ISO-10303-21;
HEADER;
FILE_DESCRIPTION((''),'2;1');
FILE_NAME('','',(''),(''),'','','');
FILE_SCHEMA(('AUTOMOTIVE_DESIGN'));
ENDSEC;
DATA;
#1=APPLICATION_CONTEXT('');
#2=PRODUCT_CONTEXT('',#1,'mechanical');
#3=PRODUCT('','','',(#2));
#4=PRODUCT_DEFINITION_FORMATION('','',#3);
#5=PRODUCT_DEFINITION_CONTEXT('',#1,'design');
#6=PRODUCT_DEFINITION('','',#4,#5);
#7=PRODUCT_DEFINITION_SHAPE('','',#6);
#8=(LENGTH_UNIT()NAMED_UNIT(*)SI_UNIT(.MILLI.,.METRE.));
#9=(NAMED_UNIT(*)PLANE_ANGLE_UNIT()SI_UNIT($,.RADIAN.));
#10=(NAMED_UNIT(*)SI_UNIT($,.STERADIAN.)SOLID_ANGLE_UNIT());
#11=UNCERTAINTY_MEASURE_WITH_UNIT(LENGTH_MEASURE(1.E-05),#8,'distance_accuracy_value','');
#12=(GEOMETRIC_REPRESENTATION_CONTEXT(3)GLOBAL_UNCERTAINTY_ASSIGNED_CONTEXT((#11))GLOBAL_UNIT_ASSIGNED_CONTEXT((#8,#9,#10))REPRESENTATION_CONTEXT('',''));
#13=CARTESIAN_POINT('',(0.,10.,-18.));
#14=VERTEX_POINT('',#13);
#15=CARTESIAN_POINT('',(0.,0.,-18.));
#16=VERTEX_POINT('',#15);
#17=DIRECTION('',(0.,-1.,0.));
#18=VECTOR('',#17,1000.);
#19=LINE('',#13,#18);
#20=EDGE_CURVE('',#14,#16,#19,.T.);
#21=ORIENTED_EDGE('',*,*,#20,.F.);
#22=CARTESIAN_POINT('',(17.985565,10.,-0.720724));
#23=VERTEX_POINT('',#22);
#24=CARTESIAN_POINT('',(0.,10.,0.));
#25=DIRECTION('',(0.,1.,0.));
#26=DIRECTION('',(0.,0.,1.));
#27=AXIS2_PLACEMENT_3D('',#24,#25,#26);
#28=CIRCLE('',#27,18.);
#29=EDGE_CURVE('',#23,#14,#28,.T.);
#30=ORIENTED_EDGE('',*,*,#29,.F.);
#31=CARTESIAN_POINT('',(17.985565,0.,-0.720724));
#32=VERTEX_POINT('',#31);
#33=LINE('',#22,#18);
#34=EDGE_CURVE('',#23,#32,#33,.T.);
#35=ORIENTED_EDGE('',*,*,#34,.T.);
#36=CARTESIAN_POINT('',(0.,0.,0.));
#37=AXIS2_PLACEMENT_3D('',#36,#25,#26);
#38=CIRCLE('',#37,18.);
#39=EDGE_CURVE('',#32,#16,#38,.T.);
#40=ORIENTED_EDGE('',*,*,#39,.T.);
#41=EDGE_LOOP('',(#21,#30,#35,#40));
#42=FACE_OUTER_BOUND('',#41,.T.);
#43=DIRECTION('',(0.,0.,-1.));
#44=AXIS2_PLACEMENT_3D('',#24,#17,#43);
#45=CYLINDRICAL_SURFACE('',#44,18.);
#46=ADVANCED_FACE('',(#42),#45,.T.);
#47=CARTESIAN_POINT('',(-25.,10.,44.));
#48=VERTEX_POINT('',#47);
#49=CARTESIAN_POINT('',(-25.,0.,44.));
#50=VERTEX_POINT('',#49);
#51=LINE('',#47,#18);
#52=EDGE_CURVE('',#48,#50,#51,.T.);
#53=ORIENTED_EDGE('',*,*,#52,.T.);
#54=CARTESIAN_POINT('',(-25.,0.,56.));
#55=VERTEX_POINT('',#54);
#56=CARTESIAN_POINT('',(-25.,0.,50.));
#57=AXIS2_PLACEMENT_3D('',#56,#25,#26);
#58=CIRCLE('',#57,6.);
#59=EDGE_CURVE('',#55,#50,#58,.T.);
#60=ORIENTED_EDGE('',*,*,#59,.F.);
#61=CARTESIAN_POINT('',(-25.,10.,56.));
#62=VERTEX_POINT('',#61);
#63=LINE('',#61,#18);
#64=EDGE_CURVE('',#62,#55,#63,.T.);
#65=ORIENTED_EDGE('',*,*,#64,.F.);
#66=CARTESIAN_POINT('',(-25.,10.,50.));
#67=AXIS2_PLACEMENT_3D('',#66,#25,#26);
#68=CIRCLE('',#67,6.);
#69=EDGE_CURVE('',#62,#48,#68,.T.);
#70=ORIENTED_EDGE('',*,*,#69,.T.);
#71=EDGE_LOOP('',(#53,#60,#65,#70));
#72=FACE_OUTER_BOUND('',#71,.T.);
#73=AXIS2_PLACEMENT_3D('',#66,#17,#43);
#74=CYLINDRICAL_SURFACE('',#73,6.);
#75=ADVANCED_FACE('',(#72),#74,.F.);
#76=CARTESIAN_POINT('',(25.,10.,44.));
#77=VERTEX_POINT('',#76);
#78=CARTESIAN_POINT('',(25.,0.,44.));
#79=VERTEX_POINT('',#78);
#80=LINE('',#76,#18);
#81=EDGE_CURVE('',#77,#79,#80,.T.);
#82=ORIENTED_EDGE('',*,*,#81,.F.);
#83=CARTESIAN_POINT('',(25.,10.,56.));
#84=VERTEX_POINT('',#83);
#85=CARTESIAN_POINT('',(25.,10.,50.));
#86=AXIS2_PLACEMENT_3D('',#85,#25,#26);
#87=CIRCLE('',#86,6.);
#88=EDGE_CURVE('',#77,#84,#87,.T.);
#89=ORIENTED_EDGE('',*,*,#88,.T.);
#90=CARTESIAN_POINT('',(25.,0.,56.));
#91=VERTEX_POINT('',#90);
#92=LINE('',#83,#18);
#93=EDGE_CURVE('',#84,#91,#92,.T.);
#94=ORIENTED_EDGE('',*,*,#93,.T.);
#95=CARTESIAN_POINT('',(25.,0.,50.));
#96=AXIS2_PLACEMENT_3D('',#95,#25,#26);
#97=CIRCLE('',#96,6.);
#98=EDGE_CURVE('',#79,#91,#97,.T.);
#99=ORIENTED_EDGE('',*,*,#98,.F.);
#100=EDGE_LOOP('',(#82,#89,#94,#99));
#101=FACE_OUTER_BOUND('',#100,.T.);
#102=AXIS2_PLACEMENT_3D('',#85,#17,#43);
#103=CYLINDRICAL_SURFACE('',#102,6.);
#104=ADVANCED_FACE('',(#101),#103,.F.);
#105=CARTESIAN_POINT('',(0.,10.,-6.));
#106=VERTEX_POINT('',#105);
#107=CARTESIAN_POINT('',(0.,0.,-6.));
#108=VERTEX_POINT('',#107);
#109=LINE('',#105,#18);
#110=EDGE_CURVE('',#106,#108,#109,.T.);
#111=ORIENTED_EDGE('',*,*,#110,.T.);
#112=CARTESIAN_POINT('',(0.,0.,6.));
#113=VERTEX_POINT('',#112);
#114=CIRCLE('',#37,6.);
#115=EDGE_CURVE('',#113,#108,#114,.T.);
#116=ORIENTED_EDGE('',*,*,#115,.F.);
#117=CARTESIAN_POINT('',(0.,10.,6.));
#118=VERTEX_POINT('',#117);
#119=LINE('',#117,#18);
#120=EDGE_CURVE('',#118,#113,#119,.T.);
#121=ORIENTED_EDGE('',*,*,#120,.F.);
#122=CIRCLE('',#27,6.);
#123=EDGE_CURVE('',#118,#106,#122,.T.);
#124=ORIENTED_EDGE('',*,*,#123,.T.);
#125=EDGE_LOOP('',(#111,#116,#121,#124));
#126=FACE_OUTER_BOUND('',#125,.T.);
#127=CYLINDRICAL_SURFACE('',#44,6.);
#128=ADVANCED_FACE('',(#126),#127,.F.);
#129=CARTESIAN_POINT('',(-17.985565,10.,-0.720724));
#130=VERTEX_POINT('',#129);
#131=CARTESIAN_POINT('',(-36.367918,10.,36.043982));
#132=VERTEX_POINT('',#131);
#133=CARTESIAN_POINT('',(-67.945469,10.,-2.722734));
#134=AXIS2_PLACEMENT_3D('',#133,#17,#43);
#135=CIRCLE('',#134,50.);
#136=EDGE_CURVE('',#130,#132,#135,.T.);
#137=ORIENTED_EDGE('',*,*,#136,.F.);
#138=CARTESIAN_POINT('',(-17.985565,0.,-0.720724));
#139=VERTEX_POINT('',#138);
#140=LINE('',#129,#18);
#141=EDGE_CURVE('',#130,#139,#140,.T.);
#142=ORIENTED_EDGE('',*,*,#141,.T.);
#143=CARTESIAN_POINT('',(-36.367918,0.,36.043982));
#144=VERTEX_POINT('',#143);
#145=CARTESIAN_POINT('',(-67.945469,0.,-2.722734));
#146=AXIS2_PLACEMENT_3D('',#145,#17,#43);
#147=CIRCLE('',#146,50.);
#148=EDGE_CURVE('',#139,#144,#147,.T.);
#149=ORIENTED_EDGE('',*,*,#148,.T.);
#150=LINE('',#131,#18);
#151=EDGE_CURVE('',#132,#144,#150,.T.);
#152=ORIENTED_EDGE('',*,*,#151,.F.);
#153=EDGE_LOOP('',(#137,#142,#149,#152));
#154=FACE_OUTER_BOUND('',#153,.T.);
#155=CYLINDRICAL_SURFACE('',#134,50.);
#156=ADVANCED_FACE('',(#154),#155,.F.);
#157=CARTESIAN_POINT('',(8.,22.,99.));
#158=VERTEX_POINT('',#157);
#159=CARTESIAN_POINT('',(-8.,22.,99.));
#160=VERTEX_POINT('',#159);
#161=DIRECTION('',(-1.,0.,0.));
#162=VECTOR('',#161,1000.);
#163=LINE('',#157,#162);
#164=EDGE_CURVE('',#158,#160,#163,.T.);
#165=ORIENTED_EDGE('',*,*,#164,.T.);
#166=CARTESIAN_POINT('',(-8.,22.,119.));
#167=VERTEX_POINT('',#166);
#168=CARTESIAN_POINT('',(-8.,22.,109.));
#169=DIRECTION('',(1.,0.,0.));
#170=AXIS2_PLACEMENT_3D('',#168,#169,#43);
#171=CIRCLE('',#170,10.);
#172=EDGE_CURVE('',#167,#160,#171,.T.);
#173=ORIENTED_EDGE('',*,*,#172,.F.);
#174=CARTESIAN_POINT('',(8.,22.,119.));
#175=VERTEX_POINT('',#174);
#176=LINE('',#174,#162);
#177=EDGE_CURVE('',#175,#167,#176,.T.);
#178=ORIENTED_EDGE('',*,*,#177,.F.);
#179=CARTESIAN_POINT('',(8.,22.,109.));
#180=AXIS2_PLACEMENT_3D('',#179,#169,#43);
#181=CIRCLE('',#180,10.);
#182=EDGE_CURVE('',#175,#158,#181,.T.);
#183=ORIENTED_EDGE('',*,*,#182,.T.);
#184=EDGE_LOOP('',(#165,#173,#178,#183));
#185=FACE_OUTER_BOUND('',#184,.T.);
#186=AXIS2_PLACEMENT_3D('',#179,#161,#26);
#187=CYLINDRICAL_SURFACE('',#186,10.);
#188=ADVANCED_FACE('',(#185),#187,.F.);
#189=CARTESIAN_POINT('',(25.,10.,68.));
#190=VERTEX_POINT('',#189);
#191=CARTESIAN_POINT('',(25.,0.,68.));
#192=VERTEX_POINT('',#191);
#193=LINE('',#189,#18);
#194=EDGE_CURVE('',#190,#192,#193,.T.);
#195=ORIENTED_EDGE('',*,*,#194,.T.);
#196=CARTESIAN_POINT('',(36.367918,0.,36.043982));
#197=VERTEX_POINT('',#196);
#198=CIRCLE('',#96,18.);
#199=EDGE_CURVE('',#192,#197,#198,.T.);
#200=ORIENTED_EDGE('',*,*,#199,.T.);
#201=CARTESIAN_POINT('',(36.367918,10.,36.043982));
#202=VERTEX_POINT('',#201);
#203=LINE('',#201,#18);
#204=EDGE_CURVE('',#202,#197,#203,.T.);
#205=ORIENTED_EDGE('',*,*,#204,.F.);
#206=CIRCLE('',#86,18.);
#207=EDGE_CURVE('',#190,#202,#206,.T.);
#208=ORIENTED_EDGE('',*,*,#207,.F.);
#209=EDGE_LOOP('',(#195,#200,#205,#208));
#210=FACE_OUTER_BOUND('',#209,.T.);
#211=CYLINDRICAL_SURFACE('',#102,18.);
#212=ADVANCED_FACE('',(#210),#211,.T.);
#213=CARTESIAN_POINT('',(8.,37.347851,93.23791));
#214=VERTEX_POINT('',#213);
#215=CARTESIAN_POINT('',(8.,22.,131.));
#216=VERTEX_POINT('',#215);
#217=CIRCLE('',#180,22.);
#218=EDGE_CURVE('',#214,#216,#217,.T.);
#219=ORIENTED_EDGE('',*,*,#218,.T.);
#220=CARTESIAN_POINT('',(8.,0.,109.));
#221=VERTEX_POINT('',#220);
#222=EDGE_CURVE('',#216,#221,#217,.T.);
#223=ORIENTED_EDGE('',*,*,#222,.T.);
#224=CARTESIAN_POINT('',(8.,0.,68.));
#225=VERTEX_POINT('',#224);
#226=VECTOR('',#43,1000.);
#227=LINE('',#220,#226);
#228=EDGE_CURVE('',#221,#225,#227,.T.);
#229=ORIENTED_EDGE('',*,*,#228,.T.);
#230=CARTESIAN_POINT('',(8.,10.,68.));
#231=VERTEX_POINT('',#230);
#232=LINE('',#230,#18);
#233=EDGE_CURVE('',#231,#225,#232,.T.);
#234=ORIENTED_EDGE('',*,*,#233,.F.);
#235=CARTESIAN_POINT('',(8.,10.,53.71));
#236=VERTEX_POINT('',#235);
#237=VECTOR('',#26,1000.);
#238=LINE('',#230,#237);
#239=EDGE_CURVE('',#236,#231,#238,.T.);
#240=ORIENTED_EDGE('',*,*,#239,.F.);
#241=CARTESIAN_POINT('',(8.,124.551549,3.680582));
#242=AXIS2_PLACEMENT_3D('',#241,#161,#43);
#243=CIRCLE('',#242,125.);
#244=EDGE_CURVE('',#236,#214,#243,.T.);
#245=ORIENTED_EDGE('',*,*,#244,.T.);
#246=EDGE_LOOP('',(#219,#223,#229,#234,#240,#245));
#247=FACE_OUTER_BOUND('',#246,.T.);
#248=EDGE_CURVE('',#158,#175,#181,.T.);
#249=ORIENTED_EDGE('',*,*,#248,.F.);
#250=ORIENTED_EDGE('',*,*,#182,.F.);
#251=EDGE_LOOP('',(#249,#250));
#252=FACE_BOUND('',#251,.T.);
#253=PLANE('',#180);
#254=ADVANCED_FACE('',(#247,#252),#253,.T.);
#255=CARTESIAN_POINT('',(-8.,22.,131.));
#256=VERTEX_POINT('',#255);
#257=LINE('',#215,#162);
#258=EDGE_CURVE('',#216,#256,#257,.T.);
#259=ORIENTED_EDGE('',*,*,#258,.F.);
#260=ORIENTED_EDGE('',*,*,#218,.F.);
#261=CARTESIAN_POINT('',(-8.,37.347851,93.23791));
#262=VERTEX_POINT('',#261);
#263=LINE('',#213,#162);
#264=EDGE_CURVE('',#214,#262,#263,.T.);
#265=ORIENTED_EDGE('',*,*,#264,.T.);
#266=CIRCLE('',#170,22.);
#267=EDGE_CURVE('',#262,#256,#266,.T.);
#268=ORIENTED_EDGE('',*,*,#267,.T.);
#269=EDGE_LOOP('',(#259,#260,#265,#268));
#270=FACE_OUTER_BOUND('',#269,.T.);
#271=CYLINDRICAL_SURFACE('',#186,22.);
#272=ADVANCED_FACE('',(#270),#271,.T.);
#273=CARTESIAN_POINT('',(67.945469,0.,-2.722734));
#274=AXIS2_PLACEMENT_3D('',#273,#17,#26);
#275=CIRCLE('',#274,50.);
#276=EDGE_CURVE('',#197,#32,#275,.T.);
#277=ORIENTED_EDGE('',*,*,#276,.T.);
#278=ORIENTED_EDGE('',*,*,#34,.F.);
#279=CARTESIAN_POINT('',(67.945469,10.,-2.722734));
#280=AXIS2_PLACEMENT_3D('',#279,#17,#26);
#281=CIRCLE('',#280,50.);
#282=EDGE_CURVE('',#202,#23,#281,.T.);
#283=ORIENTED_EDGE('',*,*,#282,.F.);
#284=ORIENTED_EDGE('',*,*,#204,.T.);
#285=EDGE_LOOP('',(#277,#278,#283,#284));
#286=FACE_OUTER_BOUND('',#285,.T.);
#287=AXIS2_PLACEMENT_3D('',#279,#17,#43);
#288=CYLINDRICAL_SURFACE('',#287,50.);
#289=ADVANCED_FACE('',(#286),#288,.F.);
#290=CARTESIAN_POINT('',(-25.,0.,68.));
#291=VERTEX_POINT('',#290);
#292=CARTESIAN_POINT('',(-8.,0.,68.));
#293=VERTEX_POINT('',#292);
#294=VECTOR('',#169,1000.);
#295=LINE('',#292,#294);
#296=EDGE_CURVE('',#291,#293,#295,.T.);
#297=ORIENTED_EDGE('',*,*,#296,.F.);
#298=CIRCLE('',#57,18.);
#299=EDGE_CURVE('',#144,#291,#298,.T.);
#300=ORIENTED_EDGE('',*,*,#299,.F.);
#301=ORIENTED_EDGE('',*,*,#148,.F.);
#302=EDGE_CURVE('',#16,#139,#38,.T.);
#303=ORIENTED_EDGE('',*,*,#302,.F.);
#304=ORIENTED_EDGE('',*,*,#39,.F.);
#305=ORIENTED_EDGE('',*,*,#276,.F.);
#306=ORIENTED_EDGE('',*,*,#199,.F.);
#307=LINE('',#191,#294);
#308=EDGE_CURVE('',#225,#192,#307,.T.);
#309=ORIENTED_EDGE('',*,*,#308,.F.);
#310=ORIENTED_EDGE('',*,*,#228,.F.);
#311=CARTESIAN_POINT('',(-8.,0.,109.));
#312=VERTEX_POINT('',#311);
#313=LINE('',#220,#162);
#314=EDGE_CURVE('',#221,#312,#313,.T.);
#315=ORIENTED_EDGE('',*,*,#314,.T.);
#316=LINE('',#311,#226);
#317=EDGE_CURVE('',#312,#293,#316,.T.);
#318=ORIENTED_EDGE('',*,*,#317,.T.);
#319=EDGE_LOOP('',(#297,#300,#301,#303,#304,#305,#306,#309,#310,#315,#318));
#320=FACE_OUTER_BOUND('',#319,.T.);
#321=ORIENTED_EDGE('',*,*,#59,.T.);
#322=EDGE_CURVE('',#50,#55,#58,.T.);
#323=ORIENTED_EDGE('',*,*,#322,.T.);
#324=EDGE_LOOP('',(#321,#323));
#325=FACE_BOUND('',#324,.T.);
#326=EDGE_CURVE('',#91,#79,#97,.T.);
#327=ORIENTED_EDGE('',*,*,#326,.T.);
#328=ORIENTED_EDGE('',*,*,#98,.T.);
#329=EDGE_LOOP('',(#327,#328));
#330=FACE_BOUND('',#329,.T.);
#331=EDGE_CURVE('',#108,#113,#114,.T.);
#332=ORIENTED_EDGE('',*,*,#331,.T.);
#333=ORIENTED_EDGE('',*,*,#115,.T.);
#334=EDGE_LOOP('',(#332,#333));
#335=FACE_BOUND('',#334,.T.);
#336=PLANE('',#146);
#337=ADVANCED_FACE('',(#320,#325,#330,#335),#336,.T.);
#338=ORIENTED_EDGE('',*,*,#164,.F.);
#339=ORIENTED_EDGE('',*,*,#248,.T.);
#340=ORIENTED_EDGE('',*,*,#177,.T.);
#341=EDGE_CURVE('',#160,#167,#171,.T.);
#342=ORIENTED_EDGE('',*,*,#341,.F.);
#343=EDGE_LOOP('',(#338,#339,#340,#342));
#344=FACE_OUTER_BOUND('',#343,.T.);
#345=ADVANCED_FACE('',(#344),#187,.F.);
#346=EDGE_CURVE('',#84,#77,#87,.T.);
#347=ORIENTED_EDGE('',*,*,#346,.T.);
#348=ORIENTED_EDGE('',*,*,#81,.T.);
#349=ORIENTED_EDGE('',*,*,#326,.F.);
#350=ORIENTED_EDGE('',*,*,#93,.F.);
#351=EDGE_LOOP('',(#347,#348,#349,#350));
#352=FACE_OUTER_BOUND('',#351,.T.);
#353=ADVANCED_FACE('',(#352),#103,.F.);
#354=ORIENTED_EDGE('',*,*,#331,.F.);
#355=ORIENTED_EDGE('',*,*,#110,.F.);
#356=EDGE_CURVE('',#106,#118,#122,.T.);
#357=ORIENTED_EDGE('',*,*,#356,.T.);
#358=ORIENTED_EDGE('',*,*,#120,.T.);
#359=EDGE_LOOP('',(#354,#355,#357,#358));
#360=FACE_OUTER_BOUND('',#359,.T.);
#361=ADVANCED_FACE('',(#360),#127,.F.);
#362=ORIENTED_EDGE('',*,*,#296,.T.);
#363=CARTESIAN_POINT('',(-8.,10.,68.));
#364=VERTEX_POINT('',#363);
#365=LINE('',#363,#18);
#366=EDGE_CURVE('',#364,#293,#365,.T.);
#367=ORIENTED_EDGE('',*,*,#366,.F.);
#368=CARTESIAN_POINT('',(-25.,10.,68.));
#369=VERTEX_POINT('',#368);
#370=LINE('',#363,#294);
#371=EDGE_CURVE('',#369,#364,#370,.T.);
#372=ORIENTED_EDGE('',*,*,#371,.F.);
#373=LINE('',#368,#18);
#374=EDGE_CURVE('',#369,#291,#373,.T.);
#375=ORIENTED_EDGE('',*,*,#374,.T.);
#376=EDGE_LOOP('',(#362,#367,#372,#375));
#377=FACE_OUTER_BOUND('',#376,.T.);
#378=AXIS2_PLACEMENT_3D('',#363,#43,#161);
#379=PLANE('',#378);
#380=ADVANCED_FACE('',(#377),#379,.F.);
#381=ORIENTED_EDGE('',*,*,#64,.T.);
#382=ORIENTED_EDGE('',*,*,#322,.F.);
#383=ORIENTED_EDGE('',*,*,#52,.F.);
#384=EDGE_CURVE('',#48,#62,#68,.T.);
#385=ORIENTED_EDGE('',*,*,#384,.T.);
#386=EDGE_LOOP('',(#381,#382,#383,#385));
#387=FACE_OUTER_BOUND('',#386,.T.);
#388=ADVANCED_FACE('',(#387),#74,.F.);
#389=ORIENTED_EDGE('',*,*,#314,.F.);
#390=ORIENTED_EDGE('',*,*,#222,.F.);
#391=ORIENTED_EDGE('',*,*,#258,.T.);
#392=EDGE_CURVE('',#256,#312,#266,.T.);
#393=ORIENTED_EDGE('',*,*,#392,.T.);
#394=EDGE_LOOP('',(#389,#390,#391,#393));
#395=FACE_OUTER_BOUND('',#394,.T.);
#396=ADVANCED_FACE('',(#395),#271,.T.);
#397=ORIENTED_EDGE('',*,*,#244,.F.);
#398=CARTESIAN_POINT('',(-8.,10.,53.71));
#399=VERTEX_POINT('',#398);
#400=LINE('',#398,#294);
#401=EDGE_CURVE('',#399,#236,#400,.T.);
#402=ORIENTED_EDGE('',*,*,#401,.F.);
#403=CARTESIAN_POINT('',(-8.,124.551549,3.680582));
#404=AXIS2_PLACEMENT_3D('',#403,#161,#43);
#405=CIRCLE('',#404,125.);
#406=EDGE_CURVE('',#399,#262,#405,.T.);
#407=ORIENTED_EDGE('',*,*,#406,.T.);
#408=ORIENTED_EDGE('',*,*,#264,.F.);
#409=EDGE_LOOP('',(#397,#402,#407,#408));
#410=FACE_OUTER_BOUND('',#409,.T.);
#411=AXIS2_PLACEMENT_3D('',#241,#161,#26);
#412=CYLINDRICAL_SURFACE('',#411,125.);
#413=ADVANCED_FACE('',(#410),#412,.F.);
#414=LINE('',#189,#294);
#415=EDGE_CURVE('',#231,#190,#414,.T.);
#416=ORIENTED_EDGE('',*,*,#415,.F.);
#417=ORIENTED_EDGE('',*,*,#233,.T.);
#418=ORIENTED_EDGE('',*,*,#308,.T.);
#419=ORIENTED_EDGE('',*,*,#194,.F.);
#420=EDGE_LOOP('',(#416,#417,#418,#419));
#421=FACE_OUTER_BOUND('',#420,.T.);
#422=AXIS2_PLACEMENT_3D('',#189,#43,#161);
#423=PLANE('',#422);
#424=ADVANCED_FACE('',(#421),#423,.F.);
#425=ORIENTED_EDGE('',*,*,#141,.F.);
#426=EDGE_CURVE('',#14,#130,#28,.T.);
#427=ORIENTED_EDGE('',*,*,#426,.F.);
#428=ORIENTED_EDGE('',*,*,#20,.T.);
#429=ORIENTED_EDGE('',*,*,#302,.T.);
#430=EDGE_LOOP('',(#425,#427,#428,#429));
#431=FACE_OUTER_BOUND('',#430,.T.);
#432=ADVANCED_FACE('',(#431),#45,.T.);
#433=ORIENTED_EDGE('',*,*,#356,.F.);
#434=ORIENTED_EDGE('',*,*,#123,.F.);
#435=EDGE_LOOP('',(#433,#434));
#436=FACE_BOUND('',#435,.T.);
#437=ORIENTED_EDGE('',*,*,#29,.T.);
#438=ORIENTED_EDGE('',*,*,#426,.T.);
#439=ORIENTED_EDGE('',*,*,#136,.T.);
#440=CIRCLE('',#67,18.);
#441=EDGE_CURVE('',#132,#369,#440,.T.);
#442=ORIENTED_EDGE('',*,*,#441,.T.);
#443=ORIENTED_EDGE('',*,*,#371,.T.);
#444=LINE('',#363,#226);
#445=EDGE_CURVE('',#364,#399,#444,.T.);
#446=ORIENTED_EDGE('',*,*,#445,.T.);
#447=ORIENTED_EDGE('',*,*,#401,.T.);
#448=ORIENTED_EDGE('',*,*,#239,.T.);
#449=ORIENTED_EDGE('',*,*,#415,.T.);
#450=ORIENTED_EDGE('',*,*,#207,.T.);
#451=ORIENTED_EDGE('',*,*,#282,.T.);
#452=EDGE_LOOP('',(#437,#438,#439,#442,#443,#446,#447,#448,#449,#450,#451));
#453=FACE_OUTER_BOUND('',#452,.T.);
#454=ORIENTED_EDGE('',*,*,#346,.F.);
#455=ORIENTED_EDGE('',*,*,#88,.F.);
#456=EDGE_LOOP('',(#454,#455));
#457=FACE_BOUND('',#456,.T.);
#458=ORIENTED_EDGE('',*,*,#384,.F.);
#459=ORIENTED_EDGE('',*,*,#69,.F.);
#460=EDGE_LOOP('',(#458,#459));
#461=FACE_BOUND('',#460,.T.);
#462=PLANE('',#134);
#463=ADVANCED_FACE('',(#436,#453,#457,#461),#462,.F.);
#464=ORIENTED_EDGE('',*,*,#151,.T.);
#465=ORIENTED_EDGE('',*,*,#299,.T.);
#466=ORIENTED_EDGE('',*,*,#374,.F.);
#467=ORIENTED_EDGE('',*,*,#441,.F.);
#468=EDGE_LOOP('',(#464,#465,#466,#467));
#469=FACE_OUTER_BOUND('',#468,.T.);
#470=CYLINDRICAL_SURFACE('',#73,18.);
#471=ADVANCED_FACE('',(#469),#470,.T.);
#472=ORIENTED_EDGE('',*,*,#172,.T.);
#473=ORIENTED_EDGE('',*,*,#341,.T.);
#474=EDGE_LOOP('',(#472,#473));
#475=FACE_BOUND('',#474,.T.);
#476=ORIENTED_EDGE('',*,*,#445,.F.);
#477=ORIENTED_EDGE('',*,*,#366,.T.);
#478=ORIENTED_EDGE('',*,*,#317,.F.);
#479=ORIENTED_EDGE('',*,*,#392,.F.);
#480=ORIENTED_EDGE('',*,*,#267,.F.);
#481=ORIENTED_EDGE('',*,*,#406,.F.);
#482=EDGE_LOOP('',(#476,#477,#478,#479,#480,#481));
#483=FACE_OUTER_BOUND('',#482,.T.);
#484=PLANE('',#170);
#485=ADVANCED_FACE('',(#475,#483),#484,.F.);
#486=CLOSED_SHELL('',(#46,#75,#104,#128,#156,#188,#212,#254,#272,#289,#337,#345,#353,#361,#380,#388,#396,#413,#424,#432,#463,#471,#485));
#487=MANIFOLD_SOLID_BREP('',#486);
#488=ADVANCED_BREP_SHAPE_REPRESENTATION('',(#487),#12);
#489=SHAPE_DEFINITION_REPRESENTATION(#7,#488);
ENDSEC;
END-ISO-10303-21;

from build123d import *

# Parameters (mm, degrees)
BASE_PLATE_SKETCH_R = 6
BASE_PLATE_DEPTH    = 10
PIVOT_LUG_SKETCH_R  = 10
PIVOT_LUG_DEPTH     = 8


with BuildPart() as part:
    # Base Plate Sketch → Base Plate (new body)
    with BuildSketch(Plane(origin=(0, 0, 0), x_dir=(1, 0, 0), z_dir=(0, 1, 0))):
        with BuildLine():
            Line((25, -68), (8, -68))
            Line((8, -68), (8, -53.71))
            Line((8, -53.71), (-8, -53.71))
            Line((-8, -53.71), (-8, -68))
            Line((-8, -68), (-25, -68))
            ThreePointArc((-25, -68), (-41.958896227, -56.032896381), (-36.367918187, -36.043982083))
            ThreePointArc((-36.367918187, -36.043982083), (-23.224109156, -19.637945422), (-17.985565246, 0.720723799))
            ThreePointArc((-17.985565246, 0.720723799), (0, 18), (17.985565246, 0.720723799))
            ThreePointArc((17.985565246, 0.720723799), (23.224109156, -19.637945422), (36.367918187, -36.043982083))
            ThreePointArc((36.367918187, -36.043982083), (41.958896227, -56.032896381), (25, -68))
        make_face()
        with Locations(Location((0, 0, 0), (0, 0, 270))):
            Circle(BASE_PLATE_SKETCH_R, mode=Mode.SUBTRACT)
        with Locations(Location((-25, -50, 0), (0, 0, 270))):
            Circle(BASE_PLATE_SKETCH_R, mode=Mode.SUBTRACT)
        with Locations(Location((25, -50, 0), (0, 0, 270))):
            Circle(BASE_PLATE_SKETCH_R, mode=Mode.SUBTRACT)
    extrude(amount=BASE_PLATE_DEPTH)

    # Pivot Lug Sketch → Pivot Lug (add, symmetric)
    with BuildSketch(Plane(origin=(0, 0, 0), x_dir=(0, 0, -1), z_dir=(1, 0, 0))):
        with BuildLine():
            Line((-109, 0), (-53.71, 0))
            Line((-53.71, 0), (-53.71, 10))
            ThreePointArc((-53.71, 10), (-74.800840464, 21.756077977), (-93.237910195, 37.347850827))
            ThreePointArc((-93.237910195, 37.347850827), (-129.268851943, 30.554159275), (-109, 0))
        make_face()
        with Locations((-109, 22)):
            Circle(PIVOT_LUG_SKETCH_R, mode=Mode.SUBTRACT)
    extrude(amount=PIVOT_LUG_DEPTH, both=True)


solid = part.part
